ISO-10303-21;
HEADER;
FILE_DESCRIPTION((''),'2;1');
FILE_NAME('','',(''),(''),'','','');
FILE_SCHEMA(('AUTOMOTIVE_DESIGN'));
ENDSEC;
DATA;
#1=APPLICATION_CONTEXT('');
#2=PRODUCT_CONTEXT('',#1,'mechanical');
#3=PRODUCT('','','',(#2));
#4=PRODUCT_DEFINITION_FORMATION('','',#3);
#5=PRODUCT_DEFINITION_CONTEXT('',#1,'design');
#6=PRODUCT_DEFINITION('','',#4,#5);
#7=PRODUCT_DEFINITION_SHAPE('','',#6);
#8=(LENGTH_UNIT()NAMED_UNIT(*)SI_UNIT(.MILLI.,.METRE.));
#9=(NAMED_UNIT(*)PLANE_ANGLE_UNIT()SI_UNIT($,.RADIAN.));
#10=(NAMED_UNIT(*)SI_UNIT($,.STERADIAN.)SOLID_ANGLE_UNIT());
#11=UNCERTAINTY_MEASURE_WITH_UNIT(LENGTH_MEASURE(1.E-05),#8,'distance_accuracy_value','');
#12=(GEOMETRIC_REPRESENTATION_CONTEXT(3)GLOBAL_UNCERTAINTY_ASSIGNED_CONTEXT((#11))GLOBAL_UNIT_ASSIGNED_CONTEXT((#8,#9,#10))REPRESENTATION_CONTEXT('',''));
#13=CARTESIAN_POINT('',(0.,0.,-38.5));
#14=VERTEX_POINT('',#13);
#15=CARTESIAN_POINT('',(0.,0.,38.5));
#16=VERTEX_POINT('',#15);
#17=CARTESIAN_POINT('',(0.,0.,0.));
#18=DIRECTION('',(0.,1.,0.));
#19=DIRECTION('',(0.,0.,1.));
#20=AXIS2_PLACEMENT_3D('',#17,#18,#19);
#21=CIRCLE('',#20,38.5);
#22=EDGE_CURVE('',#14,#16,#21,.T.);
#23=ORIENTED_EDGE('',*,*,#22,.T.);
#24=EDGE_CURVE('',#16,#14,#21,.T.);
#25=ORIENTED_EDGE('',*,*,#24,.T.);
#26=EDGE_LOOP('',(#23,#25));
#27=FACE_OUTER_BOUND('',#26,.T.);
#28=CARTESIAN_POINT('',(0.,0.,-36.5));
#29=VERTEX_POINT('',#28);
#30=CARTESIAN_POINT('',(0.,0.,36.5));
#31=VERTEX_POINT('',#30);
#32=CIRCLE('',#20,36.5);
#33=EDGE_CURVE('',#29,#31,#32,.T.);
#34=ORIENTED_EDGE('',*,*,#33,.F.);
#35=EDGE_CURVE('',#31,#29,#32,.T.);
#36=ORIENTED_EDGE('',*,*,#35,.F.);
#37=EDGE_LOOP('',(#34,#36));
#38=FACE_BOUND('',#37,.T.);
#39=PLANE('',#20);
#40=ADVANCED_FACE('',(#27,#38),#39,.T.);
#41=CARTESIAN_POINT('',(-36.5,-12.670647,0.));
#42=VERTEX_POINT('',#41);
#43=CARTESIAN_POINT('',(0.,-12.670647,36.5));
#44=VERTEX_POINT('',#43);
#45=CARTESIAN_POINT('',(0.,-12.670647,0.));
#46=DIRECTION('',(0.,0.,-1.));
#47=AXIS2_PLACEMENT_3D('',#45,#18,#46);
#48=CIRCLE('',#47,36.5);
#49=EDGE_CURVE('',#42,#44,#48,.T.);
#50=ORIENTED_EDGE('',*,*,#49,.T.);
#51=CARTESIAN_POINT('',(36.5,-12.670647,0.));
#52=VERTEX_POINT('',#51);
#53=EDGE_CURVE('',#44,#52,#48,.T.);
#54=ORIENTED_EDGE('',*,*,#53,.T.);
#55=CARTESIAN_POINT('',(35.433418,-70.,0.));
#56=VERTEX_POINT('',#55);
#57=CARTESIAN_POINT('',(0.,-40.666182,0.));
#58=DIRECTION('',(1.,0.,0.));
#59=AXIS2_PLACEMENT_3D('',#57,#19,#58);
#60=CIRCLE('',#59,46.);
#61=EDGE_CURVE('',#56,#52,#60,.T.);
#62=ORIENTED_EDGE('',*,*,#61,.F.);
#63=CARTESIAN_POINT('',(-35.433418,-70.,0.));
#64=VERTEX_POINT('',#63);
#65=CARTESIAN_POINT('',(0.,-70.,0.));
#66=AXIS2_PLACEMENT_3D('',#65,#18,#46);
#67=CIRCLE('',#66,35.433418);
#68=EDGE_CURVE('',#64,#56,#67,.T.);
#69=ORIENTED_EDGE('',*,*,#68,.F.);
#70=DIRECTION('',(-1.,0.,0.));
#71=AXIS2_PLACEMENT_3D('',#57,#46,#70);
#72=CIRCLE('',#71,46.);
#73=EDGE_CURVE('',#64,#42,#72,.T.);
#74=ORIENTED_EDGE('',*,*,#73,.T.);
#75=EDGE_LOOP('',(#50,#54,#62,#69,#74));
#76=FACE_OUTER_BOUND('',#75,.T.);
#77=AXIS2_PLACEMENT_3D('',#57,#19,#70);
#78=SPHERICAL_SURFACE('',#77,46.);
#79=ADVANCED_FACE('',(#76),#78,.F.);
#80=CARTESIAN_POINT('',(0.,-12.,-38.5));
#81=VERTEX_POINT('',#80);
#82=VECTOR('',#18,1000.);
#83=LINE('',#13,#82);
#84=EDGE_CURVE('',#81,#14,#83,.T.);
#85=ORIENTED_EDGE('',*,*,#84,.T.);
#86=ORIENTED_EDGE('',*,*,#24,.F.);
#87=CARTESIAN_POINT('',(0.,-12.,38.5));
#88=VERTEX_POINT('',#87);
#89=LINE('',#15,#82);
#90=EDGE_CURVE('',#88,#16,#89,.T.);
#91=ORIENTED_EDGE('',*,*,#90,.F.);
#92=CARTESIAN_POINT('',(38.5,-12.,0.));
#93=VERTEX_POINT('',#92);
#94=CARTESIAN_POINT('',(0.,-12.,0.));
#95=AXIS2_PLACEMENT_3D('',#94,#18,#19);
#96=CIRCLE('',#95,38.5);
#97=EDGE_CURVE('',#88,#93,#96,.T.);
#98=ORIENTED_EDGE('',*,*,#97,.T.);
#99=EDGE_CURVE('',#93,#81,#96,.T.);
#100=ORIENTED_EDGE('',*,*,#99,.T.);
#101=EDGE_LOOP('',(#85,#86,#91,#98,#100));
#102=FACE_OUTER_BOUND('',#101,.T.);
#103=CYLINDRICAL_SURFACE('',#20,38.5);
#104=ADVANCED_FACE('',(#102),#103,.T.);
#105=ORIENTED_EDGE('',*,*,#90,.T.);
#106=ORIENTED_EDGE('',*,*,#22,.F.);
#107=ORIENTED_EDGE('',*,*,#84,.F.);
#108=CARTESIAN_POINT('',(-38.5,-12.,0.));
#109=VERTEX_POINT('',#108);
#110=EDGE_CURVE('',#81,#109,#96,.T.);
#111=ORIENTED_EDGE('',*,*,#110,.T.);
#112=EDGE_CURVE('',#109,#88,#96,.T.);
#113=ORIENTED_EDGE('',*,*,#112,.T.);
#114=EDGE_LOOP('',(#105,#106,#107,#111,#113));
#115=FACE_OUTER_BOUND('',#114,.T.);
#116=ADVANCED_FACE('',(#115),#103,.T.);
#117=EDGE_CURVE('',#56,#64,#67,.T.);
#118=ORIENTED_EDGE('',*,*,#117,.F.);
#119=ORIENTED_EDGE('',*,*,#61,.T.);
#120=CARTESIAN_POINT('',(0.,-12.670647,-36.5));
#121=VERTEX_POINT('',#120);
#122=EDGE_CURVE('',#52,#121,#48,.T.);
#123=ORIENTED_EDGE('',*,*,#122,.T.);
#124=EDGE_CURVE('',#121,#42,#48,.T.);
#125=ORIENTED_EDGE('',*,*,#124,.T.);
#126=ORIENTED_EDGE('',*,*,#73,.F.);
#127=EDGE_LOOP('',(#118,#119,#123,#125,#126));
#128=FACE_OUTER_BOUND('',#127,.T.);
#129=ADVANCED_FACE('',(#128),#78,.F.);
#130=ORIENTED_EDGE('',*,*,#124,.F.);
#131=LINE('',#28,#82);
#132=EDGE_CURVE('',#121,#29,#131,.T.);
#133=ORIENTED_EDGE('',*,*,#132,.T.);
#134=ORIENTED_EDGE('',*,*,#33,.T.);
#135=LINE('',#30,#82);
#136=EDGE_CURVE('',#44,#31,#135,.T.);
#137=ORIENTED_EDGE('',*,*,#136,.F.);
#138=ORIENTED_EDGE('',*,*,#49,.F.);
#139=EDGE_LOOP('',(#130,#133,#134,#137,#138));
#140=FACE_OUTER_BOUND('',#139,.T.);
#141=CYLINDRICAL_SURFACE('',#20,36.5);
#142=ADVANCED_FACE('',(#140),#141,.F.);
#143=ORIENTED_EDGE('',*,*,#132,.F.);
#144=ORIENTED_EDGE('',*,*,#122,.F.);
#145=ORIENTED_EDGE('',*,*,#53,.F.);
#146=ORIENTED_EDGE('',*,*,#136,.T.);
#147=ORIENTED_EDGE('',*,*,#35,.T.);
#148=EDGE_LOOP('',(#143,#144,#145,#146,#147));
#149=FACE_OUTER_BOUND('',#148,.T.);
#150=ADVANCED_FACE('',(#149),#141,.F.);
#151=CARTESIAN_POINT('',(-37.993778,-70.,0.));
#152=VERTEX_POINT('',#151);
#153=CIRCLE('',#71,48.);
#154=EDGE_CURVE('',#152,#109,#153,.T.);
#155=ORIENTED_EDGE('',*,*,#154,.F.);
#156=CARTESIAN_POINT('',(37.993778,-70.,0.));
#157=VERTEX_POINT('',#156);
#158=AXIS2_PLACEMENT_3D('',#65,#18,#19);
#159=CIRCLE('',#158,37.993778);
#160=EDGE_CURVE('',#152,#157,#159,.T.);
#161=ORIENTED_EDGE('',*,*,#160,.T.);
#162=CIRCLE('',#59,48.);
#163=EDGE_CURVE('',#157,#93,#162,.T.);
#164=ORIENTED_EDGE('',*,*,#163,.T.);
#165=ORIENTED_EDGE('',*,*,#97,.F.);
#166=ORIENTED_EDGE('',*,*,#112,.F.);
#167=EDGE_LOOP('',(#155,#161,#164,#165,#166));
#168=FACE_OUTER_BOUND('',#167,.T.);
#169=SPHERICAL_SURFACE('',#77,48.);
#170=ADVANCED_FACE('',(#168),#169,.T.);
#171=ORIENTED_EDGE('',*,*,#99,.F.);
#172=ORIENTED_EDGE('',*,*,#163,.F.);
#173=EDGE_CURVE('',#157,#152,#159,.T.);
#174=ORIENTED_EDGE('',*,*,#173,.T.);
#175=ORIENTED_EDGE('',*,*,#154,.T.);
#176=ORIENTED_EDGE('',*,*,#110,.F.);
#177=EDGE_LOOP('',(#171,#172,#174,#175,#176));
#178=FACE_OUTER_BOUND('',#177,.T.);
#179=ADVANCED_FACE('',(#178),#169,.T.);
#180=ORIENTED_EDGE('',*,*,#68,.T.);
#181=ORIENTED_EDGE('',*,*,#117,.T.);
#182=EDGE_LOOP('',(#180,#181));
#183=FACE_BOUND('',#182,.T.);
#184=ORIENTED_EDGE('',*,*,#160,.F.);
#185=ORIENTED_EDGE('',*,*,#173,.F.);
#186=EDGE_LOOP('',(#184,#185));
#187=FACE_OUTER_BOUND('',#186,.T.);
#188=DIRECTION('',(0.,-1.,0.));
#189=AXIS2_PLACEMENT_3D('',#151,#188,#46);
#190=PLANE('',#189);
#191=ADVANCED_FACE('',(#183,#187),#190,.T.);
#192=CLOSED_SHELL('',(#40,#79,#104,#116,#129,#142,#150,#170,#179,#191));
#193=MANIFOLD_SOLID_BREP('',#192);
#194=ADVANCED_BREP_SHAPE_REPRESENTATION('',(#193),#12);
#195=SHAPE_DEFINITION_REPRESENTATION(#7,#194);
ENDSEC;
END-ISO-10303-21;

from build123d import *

# Parameters (mm, degrees)
SHELL_1_T = -2


with BuildPart() as part:
    # 草图1 → 旋转1 (revolve)
    with BuildSketch(Plane.XY, mode=Mode.PRIVATE) as revolve_1_sk:
        with BuildLine():
            Line((0, 0), (-38.5, 0))
            Line((-38.5, 0), (-38.5, -12))
            ThreePointArc((-38.5, -12), (-47.998171844, -41.085108941), (-37.993777534, -70))
            Line((-37.993777534, -70), (0, -70))
            Line((0, -70), (0, 0))
        make_face()
    revolve(revolve_1_sk.sketch.rotate(Axis((0, 0, 0), (0, -1, 0)), 270), axis=Axis((0, 0, 0), (0, -1, 0)))

    # 抽壳1
    shell_1_openings = [part.faces().sort_by_distance(p)[0] for p in [
        (0, -70, 0),
        (0, 0, 0),
    ]]
    offset(amount=SHELL_1_T, openings=shell_1_openings, kind=Kind.INTERSECTION)


solid = part.part
